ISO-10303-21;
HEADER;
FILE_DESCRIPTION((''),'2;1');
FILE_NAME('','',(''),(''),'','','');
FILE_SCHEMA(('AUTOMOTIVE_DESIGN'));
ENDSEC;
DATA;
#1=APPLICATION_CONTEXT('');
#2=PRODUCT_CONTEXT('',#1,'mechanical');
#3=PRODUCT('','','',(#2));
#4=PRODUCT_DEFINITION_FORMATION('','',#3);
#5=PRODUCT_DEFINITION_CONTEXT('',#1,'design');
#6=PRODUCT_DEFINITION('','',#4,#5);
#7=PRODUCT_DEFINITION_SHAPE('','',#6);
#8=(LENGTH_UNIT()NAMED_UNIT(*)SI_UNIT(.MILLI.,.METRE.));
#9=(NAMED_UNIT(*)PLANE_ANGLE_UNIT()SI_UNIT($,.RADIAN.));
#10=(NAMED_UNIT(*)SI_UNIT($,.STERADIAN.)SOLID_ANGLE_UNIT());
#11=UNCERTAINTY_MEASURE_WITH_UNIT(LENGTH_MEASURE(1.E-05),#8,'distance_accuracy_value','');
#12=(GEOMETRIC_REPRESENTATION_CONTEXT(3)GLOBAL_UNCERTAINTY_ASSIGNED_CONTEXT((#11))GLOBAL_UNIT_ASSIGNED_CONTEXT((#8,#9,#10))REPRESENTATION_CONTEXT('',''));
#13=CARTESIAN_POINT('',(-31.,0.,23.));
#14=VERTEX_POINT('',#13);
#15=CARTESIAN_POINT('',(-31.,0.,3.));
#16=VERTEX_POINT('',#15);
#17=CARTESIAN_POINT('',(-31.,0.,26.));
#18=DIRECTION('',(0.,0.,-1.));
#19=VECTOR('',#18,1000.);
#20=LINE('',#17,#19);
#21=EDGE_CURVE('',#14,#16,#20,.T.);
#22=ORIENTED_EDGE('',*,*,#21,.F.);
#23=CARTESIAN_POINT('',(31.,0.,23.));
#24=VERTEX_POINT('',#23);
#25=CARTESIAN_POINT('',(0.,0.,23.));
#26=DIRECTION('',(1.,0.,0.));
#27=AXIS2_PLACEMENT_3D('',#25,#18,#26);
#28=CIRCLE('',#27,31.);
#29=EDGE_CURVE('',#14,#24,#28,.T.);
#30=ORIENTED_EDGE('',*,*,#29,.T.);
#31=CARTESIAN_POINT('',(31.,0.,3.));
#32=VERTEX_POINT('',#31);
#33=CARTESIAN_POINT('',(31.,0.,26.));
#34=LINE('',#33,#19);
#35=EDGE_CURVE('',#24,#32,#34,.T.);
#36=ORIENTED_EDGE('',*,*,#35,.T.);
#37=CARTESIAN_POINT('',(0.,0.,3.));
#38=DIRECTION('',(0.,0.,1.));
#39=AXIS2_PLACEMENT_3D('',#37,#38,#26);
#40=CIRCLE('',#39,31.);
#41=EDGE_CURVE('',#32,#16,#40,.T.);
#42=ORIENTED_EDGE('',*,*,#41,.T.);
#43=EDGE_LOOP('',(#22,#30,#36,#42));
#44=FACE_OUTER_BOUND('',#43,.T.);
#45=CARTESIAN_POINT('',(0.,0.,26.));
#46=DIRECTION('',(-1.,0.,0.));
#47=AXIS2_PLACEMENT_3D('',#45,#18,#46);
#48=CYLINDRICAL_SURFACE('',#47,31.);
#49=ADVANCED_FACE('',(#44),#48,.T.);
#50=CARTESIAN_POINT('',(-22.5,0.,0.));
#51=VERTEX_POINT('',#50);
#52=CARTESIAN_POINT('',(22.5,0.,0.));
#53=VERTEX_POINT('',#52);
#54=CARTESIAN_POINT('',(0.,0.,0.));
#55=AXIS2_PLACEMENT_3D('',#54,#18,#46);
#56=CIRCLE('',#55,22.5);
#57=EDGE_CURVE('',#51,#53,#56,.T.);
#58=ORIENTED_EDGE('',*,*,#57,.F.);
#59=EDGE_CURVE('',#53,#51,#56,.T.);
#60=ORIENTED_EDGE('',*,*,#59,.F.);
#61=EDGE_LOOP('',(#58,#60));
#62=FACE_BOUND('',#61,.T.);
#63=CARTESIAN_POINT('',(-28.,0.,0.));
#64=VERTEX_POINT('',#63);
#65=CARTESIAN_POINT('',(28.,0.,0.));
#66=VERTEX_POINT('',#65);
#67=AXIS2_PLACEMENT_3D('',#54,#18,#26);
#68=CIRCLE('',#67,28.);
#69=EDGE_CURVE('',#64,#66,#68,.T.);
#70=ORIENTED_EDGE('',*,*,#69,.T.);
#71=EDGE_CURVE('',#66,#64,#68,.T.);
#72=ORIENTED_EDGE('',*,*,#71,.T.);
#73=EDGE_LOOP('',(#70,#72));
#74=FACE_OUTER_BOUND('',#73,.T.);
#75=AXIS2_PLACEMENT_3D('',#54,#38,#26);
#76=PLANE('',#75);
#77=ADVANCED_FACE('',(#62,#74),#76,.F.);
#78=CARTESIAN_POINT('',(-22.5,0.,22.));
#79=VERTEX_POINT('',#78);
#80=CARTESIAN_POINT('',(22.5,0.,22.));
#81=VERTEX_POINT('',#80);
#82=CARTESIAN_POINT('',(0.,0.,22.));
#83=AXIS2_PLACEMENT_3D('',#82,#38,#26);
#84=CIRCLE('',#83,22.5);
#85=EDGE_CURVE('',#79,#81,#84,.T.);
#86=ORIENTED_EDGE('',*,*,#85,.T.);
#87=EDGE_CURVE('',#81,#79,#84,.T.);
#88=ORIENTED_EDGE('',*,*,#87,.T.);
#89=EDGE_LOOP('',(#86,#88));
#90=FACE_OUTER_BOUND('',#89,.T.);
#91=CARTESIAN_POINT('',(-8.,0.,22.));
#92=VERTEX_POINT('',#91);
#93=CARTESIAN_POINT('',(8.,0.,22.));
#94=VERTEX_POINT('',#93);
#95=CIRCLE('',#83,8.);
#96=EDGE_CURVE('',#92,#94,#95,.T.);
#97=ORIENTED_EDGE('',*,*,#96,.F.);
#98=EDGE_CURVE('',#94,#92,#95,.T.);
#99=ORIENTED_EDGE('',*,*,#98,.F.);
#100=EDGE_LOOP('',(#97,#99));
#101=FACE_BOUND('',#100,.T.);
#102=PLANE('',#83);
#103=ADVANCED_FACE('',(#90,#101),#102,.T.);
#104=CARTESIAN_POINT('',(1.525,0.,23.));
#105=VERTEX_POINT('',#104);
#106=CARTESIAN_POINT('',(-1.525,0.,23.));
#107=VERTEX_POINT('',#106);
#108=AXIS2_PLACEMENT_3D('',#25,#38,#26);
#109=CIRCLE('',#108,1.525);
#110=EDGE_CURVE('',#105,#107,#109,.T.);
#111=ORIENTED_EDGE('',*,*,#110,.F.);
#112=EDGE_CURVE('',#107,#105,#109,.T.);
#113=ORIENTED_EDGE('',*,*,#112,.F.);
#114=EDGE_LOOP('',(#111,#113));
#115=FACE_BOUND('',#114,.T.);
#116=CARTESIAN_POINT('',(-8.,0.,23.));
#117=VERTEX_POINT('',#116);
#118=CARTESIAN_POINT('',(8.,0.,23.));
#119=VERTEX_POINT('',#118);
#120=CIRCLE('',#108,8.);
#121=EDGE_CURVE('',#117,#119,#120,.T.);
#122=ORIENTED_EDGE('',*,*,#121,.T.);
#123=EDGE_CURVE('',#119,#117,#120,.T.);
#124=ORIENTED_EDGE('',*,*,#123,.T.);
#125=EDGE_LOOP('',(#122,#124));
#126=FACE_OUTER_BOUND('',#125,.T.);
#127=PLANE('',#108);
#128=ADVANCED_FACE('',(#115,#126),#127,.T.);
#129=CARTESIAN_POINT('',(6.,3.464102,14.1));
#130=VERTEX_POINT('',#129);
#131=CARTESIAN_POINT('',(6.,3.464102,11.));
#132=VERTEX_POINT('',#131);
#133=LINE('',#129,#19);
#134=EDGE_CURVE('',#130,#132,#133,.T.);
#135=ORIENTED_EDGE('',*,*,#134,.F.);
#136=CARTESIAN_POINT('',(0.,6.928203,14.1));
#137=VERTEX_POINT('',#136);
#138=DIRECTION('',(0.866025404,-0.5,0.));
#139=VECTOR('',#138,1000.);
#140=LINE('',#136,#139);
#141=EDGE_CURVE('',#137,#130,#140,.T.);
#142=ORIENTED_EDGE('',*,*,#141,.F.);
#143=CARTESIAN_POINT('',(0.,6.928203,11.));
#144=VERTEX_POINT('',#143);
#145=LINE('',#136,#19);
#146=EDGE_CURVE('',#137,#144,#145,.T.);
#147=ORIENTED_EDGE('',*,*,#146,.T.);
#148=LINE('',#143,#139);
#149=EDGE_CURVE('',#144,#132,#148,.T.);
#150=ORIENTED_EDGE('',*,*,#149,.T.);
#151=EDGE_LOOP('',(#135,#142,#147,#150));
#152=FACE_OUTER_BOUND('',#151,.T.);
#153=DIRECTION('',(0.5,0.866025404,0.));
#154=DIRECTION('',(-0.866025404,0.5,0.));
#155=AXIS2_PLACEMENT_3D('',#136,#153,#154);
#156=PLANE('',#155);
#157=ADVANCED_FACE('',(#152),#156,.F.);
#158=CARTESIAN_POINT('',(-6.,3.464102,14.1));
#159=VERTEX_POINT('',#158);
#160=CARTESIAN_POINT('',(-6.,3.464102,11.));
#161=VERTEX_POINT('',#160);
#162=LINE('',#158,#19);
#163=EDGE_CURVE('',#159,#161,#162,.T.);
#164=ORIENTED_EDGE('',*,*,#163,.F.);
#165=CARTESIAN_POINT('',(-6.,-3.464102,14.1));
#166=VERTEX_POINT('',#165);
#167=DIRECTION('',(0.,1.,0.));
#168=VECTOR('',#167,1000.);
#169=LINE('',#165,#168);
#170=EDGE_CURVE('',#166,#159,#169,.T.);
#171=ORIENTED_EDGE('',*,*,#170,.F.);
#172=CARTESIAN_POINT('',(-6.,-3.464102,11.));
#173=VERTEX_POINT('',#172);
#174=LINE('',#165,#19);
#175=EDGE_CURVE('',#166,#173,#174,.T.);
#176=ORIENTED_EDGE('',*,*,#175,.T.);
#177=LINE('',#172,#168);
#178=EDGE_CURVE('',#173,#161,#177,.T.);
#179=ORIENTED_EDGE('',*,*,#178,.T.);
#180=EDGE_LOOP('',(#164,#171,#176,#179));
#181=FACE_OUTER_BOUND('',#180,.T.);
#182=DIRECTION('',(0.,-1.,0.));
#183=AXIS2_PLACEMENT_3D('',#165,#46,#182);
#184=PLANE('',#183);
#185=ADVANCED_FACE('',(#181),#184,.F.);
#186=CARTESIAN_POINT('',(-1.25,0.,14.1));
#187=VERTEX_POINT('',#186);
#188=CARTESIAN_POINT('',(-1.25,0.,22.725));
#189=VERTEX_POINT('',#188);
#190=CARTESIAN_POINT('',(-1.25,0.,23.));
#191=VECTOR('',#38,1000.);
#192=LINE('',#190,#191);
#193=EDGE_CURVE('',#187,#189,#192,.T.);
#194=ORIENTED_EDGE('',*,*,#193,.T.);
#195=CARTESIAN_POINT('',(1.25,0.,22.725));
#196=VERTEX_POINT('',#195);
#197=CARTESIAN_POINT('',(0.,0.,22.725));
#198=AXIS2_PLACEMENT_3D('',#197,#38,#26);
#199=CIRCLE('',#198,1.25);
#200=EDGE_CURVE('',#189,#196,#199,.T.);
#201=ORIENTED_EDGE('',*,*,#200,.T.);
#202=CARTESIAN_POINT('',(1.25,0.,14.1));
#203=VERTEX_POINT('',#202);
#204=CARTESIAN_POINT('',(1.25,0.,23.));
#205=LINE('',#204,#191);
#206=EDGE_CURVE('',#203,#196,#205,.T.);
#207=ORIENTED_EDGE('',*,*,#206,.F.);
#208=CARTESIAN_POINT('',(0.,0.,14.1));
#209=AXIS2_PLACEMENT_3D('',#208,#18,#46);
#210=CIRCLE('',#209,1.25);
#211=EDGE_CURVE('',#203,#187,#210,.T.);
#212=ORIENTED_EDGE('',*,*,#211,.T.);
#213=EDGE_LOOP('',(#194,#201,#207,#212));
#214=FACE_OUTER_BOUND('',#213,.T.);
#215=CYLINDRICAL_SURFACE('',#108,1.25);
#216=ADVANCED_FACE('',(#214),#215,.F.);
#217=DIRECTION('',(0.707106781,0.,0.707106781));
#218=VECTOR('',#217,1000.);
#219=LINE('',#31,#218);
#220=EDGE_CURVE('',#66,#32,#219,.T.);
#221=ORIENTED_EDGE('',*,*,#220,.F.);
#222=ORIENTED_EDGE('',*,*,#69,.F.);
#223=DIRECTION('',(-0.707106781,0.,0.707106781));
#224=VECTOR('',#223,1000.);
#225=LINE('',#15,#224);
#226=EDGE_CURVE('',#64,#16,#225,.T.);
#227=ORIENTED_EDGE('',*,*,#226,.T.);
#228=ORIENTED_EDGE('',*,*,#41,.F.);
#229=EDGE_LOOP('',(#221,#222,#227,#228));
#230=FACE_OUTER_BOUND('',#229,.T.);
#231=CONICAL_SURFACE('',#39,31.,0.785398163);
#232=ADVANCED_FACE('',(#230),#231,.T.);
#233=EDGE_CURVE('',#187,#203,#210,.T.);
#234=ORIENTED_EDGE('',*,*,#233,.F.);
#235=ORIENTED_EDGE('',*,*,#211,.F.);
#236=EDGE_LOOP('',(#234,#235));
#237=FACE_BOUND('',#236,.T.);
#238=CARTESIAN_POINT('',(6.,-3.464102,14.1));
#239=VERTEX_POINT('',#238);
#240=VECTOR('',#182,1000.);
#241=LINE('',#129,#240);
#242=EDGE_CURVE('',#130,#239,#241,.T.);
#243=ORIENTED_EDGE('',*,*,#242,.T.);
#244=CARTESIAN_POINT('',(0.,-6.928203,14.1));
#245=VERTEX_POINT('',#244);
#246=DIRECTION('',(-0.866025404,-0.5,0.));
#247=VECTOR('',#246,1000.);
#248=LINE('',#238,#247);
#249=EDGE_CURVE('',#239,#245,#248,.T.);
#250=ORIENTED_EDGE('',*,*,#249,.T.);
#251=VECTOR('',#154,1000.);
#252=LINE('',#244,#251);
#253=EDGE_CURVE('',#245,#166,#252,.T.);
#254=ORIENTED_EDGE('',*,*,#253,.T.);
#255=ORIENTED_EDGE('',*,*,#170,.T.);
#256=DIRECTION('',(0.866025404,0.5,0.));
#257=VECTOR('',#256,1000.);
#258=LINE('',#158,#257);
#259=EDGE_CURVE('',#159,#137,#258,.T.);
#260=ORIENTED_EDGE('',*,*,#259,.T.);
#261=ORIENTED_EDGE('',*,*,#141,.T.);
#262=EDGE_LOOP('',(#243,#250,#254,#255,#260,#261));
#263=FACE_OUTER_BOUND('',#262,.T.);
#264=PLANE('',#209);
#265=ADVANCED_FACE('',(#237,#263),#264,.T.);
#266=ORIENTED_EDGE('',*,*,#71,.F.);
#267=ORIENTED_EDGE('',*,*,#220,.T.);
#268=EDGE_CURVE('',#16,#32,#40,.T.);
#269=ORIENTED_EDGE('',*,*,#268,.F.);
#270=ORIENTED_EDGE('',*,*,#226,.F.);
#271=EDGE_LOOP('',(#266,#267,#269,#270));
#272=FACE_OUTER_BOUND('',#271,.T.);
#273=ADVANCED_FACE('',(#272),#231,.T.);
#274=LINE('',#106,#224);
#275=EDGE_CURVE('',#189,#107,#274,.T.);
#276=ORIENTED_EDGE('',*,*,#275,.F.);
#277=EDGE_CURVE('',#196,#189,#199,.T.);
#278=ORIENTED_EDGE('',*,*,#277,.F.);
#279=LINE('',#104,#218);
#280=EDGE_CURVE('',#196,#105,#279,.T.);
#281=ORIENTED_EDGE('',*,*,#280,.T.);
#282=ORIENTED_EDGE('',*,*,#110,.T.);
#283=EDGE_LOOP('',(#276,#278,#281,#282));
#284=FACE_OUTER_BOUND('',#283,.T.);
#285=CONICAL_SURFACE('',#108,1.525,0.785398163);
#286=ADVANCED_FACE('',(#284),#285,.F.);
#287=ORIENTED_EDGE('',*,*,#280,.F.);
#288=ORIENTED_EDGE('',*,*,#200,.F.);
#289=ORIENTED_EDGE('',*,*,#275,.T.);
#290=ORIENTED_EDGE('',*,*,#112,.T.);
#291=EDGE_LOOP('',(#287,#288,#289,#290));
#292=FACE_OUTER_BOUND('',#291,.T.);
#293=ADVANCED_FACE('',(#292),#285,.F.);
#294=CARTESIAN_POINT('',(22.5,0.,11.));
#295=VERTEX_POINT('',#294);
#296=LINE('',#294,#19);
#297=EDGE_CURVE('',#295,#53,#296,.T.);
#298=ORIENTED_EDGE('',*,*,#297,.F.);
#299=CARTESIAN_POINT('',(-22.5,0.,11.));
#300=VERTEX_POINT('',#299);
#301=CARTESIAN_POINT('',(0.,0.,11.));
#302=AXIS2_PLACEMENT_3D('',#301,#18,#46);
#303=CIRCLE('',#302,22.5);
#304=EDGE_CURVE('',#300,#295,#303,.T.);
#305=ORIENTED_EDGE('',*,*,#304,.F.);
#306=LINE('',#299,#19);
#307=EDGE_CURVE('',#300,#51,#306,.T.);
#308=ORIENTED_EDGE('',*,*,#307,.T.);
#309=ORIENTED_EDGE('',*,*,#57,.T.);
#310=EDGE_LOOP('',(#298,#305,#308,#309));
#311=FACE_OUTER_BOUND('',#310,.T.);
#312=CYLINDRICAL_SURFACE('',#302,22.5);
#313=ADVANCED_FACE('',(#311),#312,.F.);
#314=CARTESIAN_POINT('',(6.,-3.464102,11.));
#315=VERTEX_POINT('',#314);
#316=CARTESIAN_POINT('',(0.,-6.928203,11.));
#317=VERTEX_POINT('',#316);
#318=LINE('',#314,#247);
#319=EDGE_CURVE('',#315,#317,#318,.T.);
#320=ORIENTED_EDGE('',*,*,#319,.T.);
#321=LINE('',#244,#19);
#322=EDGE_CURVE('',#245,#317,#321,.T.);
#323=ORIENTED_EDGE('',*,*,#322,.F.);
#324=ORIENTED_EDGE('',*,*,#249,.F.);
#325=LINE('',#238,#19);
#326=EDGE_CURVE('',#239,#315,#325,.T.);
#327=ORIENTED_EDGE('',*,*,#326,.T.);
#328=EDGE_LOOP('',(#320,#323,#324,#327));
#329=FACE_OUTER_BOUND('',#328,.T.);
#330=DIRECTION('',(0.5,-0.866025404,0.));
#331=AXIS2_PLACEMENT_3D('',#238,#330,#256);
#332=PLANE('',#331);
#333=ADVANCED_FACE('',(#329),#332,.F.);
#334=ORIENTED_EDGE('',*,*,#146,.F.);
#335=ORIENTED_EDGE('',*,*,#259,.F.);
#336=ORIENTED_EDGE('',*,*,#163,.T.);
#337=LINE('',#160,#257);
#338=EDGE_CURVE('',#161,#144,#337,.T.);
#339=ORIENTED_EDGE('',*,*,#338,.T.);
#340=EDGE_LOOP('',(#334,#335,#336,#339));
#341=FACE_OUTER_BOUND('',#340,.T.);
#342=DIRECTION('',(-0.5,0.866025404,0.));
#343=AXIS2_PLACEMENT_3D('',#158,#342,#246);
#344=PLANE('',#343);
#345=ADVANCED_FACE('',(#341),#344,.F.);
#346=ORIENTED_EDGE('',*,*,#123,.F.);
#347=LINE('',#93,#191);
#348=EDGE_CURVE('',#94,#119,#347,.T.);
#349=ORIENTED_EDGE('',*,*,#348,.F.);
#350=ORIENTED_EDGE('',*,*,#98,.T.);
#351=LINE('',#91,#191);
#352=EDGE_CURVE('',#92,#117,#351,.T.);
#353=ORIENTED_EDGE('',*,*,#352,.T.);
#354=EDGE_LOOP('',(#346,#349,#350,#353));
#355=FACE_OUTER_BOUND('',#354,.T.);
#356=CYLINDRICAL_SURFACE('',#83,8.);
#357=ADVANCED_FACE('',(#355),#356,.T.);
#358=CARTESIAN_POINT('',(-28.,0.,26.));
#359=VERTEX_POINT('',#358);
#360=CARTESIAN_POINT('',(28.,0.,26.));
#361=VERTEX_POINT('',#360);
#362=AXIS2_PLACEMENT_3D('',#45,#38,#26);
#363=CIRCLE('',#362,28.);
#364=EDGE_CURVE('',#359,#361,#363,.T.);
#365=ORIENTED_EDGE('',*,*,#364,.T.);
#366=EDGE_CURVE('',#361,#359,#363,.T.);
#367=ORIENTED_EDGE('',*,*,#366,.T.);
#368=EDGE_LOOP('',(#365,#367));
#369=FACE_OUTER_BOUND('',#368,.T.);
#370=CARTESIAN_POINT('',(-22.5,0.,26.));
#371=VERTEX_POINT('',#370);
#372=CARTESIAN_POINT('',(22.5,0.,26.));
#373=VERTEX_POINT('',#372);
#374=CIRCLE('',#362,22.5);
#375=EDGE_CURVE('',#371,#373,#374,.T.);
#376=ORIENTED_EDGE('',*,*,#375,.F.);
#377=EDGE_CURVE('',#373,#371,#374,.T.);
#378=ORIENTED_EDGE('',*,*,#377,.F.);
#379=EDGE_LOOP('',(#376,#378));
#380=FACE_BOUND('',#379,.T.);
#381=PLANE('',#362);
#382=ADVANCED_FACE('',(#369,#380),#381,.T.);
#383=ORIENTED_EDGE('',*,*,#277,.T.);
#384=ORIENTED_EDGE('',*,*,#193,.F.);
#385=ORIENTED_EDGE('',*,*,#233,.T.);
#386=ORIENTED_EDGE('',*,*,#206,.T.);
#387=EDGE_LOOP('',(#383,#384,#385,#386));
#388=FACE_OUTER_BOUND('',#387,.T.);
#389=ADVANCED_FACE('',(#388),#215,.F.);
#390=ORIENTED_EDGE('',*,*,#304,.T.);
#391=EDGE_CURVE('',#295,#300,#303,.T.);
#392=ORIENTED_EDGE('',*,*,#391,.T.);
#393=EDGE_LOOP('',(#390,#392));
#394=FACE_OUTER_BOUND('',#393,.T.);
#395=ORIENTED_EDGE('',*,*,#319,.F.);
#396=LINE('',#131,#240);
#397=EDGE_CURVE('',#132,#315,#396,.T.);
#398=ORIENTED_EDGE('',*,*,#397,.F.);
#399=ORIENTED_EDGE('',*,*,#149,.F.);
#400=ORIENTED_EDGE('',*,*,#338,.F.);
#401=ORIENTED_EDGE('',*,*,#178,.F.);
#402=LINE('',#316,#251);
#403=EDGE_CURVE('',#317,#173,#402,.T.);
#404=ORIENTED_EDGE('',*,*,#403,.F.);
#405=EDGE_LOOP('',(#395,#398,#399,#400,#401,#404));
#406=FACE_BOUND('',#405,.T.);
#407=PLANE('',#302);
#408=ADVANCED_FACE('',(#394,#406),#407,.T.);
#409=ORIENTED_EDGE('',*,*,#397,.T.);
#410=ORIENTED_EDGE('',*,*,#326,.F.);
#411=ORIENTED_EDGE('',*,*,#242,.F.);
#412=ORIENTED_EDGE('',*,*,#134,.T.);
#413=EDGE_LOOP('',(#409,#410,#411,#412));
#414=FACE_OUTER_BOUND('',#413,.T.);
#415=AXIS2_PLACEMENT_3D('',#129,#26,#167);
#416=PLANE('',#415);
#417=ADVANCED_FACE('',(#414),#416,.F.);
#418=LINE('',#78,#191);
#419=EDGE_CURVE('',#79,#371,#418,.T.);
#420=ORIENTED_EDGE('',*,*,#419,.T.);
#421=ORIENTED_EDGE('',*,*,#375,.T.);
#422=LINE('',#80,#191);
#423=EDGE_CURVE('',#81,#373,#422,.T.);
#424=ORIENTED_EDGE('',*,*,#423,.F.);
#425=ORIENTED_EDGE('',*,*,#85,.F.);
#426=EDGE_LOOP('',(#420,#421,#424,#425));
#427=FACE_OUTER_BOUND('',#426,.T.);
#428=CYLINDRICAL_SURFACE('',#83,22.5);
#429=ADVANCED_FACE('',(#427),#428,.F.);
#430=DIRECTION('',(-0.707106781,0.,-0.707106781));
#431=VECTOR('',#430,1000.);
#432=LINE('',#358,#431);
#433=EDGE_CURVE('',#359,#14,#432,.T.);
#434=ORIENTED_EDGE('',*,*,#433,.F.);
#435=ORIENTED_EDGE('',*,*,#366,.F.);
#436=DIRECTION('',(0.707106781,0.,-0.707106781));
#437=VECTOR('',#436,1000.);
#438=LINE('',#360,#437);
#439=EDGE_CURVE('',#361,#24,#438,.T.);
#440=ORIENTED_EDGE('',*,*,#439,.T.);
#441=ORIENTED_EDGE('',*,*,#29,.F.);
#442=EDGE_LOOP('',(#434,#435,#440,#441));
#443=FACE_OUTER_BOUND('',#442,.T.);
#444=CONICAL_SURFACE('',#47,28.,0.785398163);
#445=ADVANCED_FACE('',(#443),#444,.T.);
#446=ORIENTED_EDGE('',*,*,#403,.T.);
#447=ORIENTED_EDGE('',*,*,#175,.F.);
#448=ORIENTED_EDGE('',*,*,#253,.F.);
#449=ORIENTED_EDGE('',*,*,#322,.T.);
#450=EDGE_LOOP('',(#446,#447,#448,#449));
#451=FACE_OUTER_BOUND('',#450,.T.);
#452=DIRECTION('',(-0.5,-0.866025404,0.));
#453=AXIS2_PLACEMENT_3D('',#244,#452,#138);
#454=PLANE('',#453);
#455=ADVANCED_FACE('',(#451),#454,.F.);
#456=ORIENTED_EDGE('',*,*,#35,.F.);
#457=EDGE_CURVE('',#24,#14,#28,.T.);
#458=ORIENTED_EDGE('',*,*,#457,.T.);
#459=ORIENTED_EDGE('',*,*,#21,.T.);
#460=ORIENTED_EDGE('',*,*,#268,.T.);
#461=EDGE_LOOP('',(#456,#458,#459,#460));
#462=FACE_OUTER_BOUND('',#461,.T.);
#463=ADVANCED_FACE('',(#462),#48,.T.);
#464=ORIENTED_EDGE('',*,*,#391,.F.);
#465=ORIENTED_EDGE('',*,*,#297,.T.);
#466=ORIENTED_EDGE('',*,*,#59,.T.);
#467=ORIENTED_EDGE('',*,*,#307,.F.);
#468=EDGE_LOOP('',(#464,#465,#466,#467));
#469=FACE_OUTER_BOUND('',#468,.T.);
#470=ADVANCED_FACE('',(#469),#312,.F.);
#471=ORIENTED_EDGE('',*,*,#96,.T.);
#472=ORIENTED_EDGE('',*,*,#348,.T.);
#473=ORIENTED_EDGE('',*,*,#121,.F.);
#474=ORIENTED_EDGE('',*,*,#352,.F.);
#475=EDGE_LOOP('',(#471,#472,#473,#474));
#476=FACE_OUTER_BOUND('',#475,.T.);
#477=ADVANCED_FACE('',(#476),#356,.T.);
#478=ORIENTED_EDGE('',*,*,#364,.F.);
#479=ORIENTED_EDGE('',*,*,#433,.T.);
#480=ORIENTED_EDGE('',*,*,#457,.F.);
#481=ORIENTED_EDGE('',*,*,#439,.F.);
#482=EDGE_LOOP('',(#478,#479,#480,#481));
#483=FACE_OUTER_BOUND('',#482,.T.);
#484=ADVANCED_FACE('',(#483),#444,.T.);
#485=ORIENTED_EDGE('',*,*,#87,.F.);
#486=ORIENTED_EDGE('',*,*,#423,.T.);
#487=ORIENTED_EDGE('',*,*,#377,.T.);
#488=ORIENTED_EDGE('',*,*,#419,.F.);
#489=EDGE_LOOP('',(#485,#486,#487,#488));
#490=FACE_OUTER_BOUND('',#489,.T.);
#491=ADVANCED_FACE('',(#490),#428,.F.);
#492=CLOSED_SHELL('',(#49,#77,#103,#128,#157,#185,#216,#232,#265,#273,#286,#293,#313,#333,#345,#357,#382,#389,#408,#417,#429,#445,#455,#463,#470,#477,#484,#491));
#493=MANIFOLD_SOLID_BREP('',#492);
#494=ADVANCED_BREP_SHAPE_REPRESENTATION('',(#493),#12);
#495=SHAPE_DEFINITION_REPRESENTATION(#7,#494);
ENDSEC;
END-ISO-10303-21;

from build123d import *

# Parameters (mm, degrees)
SKETCH1_R                   = 31
BOSS_EXTRUDE1_DEPTH         = 26
SKETCH2_R                   = 22.5
CUT_EXTRUDE1_DEPTH          = 11
CUT_EXTRUDE2_DEPTH          = 3.1
CUT_EXTRUDE3_START          = -4
SKETCH4_R                   = 22.5
SKETCH4_R_2                 = 8
CUT_EXTRUDE3_DEPTH          = 4
CUT_EXTRUDE4_START          = -3
SKETCH5_R                   = 8
CUT_EXTRUDE4_DEPTH          = 3
M3_TAPPED_HOLE1_D           = 2.5
M3_TAPPED_HOLE1_CSINK_D     = 3.05
M3_TAPPED_HOLE1_CSINK_ANGLE = 90
CHAMFER1_SIZE               = 3


with BuildPart() as part:
    # Sketch1 → Boss-Extrude1 (new body)
    with BuildSketch(Plane.XY):
        with Locations(Location((0, 0, 0), (0, 0, 180))):
            Circle(SKETCH1_R)
    extrude(amount=BOSS_EXTRUDE1_DEPTH)

    # Sketch2 → Cut-Extrude1 (cut)
    with BuildSketch(Plane(origin=(0, 0, 0), x_dir=(-1, 0, 0), z_dir=(0, 0, -1))):
        Circle(SKETCH2_R)
    extrude(amount=-CUT_EXTRUDE1_DEPTH, mode=Mode.SUBTRACT)

    # Sketch3 → Cut-Extrude2 (cut)
    with BuildSketch(Plane(origin=(0, 0, 11), x_dir=(-1, 0, 0), z_dir=(0, 0, -1))):
        Polygon((0, 6.92820323), (-6, 3.464101615), (-6, -3.464101615), (0, -6.92820323), (6, -3.464101615), (6, 3.464101615), align=None)
    extrude(amount=-CUT_EXTRUDE2_DEPTH, mode=Mode.SUBTRACT)

    # Sketch4 → Cut-Extrude3 (cut)
    with BuildSketch(Plane.XY.offset(26).offset(CUT_EXTRUDE3_START)):
        with Locations(Location((0, 0, 0), (0, 0, 180))):
            Circle(SKETCH4_R)
        Circle(SKETCH4_R_2, mode=Mode.SUBTRACT)
    extrude(amount=CUT_EXTRUDE3_DEPTH, mode=Mode.SUBTRACT)

    # Sketch5 → Cut-Extrude4 (cut)
    with BuildSketch(Plane.XY.offset(26).offset(CUT_EXTRUDE4_START)):
        Circle(SKETCH5_R)
    extrude(amount=CUT_EXTRUDE4_DEPTH, mode=Mode.SUBTRACT)

    # M3 Tapped Hole1 (through all)
    with Locations(Plane.XY.offset(23)):
        with Locations((0, 0)):
            CounterSinkHole(M3_TAPPED_HOLE1_D / 2, M3_TAPPED_HOLE1_CSINK_D / 2, counter_sink_angle=M3_TAPPED_HOLE1_CSINK_ANGLE)

    # Chamfer1
    chamfer1_edges = [part.edges().sort_by_distance(p)[0] for p in [
        (31, 0, 0),
        (31, 0, 26),
    ]]
    chamfer(chamfer1_edges, length=CHAMFER1_SIZE)


solid = part.part
